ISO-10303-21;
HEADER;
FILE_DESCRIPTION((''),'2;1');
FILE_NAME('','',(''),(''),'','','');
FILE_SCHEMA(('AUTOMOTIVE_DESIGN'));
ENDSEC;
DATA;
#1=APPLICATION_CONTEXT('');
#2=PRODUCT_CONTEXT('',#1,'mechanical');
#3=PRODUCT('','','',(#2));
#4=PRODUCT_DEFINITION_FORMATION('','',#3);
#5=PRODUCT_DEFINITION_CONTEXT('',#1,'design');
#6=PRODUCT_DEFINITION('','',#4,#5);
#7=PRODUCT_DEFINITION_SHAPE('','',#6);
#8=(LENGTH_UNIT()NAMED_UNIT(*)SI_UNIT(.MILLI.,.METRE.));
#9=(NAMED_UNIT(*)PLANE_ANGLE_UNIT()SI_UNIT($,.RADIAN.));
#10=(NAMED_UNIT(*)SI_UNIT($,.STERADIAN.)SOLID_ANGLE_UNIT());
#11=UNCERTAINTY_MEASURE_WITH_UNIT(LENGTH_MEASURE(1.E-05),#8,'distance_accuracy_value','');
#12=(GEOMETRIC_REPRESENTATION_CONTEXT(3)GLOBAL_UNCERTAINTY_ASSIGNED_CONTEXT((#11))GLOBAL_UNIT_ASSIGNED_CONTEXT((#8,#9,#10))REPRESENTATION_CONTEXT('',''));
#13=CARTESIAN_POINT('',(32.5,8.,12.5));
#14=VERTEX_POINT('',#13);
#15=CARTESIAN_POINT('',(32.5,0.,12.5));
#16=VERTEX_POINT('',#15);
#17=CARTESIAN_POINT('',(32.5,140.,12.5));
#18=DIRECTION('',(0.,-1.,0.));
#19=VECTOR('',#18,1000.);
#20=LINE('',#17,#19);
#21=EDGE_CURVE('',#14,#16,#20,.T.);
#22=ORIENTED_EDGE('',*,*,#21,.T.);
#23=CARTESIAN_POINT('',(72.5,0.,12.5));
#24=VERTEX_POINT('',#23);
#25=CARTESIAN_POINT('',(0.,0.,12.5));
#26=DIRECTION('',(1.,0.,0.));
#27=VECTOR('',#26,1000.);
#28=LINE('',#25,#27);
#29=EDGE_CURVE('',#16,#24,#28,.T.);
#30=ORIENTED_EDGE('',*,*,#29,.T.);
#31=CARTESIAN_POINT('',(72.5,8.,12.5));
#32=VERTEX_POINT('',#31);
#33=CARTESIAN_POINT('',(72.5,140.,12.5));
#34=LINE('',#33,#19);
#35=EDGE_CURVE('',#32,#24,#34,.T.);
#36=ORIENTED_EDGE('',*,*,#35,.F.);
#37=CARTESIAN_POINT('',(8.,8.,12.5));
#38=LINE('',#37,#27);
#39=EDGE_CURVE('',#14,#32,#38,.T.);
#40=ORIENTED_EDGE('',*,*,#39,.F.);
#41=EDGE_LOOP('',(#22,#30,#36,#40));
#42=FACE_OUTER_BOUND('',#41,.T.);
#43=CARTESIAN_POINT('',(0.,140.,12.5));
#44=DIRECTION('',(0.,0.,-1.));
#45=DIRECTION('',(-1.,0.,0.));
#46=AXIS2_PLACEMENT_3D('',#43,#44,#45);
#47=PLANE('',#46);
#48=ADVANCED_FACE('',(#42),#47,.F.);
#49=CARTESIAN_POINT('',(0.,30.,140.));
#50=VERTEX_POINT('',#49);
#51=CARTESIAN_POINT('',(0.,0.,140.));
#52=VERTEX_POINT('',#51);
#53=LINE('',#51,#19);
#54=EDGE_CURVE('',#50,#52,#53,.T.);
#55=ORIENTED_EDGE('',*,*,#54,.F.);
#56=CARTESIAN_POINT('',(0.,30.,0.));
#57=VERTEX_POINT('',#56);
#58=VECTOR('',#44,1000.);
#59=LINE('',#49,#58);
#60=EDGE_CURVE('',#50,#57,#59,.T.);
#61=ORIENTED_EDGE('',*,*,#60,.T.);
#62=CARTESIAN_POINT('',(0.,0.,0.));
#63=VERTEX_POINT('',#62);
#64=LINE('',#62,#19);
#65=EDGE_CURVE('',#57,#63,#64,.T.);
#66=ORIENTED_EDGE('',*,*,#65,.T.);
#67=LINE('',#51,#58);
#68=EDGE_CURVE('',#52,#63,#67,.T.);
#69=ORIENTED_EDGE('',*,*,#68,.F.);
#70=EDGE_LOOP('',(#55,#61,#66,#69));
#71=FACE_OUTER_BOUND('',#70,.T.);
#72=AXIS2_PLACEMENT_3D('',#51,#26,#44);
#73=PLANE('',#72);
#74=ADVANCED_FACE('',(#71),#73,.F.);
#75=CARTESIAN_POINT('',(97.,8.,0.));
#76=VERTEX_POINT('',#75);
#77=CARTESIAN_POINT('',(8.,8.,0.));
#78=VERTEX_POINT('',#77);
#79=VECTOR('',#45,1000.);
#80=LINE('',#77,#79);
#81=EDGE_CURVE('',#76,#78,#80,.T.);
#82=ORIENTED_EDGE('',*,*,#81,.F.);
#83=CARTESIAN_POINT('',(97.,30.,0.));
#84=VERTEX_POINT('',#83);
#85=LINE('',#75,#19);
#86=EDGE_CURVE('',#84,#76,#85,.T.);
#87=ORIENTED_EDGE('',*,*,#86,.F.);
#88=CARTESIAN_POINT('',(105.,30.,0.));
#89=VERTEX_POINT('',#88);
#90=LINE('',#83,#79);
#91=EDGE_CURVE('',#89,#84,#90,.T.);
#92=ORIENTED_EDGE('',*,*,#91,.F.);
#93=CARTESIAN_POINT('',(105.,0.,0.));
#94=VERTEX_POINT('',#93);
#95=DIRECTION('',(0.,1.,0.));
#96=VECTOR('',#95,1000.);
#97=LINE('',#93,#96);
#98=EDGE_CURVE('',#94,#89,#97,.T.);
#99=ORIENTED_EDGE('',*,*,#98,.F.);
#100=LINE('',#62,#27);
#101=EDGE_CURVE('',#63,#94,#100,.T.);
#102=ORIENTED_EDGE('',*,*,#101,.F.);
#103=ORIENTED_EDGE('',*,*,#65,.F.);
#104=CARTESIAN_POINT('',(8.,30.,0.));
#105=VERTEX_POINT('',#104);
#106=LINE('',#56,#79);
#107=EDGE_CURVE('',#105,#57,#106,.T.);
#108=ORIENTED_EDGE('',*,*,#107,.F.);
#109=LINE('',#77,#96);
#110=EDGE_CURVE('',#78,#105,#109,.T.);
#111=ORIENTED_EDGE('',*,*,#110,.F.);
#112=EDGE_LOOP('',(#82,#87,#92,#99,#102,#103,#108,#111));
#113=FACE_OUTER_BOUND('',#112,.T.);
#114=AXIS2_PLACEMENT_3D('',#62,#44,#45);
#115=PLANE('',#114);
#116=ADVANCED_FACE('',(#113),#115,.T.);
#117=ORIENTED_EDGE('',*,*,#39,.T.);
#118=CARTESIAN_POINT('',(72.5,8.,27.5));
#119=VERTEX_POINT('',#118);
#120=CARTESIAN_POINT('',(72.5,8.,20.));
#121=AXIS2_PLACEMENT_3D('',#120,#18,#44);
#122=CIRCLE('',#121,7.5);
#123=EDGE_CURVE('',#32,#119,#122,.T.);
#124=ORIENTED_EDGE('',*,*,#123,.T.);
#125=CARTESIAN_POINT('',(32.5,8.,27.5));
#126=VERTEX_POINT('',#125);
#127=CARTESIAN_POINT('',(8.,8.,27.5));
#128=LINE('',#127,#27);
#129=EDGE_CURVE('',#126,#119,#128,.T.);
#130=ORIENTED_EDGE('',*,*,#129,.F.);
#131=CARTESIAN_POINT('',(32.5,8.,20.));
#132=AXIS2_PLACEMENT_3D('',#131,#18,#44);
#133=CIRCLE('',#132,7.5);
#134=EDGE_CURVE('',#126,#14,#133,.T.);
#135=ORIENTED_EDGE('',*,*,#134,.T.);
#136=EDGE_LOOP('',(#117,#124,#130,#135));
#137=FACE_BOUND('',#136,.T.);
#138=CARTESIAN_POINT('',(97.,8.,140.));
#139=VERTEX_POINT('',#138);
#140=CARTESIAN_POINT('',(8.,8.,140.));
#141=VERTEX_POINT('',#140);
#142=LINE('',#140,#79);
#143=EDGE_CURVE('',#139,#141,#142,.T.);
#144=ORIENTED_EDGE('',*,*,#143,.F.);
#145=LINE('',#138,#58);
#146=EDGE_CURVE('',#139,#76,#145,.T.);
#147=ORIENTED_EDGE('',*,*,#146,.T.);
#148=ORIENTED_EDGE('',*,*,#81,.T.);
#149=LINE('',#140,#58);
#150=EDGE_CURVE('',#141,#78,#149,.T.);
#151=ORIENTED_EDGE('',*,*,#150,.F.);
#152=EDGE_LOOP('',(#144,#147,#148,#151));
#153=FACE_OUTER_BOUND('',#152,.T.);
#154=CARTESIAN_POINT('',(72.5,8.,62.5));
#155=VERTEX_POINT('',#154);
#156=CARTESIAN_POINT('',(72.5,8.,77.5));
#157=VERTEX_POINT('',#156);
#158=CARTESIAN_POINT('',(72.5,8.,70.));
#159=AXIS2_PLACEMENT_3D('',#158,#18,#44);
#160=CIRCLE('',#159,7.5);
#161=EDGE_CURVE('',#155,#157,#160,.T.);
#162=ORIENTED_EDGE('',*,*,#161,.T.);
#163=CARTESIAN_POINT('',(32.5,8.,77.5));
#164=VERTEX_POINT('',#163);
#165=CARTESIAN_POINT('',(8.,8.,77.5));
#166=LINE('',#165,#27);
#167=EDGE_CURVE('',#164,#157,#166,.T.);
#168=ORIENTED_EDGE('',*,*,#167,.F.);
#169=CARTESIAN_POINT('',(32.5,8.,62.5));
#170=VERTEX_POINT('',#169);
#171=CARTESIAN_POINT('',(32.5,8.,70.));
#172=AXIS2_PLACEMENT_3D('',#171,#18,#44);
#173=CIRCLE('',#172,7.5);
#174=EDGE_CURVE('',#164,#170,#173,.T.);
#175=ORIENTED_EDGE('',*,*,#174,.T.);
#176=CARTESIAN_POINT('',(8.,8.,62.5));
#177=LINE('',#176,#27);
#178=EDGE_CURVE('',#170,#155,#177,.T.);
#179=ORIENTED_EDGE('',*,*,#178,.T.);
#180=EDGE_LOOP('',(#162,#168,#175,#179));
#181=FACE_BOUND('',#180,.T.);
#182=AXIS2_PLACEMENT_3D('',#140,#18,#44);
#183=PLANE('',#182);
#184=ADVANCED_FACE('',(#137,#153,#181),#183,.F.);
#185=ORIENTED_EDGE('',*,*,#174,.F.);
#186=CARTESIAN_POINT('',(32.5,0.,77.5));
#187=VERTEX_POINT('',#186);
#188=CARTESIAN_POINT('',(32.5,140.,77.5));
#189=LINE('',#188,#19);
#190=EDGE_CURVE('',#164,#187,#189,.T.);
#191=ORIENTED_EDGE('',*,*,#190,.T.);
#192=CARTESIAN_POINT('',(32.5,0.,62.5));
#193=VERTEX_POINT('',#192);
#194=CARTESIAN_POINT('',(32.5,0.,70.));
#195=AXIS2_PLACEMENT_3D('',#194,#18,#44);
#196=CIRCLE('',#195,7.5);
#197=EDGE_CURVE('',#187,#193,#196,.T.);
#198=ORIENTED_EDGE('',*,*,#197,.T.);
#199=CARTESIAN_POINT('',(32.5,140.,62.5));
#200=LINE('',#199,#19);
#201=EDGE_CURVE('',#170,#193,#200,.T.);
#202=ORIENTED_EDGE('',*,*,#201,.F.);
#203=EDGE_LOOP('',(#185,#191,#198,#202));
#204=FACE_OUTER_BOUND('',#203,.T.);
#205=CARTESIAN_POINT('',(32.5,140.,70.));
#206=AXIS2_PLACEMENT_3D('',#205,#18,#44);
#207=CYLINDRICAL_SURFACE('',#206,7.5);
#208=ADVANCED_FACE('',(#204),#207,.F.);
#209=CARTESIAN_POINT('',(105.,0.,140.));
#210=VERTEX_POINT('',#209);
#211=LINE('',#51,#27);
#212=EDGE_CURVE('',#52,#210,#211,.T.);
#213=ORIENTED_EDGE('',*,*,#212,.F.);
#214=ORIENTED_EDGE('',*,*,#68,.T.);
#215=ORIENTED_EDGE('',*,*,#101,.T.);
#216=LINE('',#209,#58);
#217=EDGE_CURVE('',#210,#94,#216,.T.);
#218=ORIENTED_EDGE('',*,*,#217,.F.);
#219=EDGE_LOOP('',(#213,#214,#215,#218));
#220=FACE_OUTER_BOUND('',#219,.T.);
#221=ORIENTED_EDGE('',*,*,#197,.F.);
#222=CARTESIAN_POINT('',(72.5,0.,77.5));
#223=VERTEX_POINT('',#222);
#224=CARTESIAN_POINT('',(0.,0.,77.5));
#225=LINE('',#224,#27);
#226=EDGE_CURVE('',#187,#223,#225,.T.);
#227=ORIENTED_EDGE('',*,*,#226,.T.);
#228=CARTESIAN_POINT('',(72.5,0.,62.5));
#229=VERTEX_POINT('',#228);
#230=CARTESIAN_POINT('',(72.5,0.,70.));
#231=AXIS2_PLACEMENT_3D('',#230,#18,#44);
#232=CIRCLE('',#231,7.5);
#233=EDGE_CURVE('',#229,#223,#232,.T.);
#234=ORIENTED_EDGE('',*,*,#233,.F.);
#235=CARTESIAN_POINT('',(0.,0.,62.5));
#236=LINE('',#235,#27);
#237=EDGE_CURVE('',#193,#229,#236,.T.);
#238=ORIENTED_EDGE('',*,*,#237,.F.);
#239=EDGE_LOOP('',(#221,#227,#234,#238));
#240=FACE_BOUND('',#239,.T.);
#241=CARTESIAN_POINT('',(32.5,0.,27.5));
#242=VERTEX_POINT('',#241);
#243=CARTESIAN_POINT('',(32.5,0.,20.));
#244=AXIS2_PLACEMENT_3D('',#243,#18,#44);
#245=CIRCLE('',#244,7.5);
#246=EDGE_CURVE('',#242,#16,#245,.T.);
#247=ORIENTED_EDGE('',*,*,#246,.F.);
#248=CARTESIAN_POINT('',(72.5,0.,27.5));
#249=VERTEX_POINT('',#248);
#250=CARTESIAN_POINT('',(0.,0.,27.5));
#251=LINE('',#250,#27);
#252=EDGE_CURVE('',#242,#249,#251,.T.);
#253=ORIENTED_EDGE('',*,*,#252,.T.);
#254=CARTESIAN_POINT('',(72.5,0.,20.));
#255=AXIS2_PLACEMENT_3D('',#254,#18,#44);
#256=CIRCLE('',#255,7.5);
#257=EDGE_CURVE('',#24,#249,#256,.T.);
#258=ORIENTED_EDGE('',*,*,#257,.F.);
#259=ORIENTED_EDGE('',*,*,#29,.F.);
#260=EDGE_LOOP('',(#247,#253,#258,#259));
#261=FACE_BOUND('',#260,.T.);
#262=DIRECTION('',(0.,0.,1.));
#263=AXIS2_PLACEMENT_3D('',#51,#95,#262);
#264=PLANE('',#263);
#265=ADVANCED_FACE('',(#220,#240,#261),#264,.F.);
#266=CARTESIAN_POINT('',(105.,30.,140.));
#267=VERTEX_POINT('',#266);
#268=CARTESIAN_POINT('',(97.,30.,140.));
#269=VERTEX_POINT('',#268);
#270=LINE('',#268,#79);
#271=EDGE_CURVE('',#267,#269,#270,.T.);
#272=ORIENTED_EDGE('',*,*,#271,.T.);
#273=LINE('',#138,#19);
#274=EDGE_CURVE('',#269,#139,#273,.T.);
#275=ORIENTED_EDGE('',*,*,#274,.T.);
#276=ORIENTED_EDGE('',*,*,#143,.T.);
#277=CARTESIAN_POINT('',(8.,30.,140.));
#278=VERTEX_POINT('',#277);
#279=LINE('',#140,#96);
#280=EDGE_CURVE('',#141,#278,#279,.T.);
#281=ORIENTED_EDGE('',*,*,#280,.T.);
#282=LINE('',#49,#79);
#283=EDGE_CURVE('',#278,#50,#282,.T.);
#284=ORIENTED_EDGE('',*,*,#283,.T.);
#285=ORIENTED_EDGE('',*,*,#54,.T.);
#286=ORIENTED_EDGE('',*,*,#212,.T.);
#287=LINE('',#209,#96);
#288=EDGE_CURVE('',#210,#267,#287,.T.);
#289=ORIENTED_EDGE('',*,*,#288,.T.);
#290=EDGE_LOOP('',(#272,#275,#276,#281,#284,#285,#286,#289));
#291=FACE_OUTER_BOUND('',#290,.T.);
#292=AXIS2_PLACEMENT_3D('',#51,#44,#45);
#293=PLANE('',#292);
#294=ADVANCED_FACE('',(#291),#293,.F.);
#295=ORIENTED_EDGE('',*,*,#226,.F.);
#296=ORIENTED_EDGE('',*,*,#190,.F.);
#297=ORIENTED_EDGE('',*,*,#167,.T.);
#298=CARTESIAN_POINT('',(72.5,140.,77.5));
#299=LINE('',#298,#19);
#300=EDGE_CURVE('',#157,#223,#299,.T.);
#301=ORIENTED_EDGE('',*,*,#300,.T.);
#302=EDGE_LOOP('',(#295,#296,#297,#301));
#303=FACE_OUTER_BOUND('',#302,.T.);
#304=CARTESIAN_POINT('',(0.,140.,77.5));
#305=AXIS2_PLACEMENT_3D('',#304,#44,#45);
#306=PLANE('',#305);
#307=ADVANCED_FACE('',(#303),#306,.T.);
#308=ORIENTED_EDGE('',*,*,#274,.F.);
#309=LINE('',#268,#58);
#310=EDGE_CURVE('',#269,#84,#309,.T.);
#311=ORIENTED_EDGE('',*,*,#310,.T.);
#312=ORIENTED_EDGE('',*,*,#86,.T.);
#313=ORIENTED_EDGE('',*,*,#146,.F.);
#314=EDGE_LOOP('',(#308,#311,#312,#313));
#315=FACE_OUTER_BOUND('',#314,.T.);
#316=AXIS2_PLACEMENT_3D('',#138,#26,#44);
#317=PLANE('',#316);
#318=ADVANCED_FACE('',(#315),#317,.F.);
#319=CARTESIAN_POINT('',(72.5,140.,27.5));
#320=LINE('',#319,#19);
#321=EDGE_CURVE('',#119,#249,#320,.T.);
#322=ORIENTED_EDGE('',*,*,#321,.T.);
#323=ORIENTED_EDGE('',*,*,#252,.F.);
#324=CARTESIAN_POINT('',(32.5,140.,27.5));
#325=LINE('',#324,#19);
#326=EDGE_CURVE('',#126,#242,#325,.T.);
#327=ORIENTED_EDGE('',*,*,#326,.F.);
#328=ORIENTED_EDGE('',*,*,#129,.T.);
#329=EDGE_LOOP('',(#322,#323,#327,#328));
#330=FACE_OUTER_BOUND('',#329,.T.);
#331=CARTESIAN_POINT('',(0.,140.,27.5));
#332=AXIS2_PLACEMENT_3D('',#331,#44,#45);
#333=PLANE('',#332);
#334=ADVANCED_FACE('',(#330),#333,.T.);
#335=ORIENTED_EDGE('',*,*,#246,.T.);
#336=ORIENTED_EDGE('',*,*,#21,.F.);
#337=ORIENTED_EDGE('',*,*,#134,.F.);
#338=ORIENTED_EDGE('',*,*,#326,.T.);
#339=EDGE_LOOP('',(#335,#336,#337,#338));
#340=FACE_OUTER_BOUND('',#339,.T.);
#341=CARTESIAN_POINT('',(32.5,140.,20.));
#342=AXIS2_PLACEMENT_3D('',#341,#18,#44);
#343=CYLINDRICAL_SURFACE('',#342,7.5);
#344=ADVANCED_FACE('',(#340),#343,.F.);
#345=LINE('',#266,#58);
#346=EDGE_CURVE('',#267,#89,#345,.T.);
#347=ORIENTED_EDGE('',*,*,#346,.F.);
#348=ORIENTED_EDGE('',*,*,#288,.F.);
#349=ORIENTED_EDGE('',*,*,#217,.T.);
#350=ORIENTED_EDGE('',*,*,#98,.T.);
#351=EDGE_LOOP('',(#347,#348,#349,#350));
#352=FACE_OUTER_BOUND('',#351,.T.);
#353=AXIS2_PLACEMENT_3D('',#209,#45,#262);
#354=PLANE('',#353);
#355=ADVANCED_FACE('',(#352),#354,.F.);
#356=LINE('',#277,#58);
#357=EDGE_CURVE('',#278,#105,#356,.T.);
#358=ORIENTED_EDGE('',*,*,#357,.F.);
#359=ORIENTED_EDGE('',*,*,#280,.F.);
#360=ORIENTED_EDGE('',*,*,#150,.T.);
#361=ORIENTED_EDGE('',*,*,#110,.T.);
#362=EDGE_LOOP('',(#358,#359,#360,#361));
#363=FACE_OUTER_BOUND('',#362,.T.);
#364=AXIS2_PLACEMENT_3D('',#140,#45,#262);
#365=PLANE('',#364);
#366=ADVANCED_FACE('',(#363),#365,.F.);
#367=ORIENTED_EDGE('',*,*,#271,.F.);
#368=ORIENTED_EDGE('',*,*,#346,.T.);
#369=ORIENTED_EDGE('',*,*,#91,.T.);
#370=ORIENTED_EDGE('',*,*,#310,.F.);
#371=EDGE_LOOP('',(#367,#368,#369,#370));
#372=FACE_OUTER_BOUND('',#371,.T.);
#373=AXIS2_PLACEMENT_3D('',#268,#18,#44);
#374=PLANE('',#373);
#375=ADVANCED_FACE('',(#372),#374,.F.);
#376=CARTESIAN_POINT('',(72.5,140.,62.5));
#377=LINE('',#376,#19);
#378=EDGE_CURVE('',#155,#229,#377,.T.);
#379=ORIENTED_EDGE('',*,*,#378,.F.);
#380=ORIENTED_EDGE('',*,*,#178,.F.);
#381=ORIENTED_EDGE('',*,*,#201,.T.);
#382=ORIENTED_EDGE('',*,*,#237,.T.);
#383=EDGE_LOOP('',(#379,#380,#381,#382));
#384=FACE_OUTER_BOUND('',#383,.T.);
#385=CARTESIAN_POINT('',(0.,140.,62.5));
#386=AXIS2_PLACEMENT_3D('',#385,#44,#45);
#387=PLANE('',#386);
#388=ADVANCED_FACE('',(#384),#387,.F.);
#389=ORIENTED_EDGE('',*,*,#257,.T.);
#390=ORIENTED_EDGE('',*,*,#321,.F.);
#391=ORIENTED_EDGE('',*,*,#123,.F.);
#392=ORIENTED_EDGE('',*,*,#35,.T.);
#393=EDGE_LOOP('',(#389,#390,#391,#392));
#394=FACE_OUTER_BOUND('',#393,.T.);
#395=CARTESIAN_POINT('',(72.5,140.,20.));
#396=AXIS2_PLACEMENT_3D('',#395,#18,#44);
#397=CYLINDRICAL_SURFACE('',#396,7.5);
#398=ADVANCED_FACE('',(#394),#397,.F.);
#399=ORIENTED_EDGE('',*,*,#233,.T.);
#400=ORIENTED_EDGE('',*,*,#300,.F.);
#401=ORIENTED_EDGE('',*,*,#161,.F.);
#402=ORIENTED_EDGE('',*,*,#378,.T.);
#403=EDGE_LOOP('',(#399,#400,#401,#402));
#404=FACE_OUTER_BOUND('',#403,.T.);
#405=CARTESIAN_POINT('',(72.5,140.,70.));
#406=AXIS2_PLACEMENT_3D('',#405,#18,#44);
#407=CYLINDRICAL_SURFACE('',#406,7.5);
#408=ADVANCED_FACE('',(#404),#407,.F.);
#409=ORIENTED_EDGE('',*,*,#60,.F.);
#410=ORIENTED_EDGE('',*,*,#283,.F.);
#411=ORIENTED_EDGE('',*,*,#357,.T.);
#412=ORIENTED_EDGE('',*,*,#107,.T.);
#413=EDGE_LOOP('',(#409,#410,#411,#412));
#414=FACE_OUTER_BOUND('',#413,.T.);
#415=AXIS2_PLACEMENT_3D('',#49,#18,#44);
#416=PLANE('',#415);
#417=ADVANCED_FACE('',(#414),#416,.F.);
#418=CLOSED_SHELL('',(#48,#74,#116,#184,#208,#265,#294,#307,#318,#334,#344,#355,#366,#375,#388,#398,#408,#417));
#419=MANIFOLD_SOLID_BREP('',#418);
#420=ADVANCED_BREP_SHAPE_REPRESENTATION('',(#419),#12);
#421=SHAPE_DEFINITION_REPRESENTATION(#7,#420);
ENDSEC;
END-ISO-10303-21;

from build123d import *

# Parameters (mm, degrees)
EXTRUDE_1_DEPTH     = 140
CUT_EXTRUDE_1_DEPTH = 140


with BuildPart() as part:
    # 草图1 → 凸台-拉伸1 (new body)
    with BuildSketch(Plane.XY):
        Polygon((0, 0), (105, 0), (105, 30), (97, 30), (97, 8), (8, 8), (8, 30), (0, 30), align=None)
    extrude(amount=EXTRUDE_1_DEPTH)

    # 草图2 → 切除-拉伸1 (cut)
    with BuildSketch(Plane.XZ):
        with BuildLine():
            Line((52.5, 70), (52.5, 62.5))
            Line((52.5, 62.5), (72.5, 62.5))
            ThreePointArc((72.5, 62.5), (80, 70), (72.5, 77.5))
            Line((72.5, 77.5), (52.5, 77.5))
            Line((52.5, 77.5), (52.5, 70))
        make_face()
        with BuildLine():
            Line((32.5, 62.5), (52.5, 62.5))
            Line((52.5, 62.5), (52.5, 70))
            Line((52.5, 70), (52.5, 77.5))
            Line((52.5, 77.5), (32.5, 77.5))
            ThreePointArc((32.5, 77.5), (25, 70), (32.5, 62.5))
        make_face()
        with BuildLine():
            Line((32.5, 12.5), (52.5, 12.5))
            Line((52.5, 12.5), (52.5, 20))
            Line((52.5, 20), (52.5, 27.5))
            Line((52.5, 27.5), (32.5, 27.5))
            ThreePointArc((32.5, 27.5), (25, 20), (32.5, 12.5))
        make_face()
        with BuildLine():
            Line((52.5, 20), (52.5, 12.5))
            Line((52.5, 12.5), (72.5, 12.5))
            ThreePointArc((72.5, 12.5), (80, 20), (72.5, 27.5))
            Line((72.5, 27.5), (52.5, 27.5))
            Line((52.5, 27.5), (52.5, 20))
        make_face()
    extrude(amount=-CUT_EXTRUDE_1_DEPTH, mode=Mode.SUBTRACT)


solid = part.part
